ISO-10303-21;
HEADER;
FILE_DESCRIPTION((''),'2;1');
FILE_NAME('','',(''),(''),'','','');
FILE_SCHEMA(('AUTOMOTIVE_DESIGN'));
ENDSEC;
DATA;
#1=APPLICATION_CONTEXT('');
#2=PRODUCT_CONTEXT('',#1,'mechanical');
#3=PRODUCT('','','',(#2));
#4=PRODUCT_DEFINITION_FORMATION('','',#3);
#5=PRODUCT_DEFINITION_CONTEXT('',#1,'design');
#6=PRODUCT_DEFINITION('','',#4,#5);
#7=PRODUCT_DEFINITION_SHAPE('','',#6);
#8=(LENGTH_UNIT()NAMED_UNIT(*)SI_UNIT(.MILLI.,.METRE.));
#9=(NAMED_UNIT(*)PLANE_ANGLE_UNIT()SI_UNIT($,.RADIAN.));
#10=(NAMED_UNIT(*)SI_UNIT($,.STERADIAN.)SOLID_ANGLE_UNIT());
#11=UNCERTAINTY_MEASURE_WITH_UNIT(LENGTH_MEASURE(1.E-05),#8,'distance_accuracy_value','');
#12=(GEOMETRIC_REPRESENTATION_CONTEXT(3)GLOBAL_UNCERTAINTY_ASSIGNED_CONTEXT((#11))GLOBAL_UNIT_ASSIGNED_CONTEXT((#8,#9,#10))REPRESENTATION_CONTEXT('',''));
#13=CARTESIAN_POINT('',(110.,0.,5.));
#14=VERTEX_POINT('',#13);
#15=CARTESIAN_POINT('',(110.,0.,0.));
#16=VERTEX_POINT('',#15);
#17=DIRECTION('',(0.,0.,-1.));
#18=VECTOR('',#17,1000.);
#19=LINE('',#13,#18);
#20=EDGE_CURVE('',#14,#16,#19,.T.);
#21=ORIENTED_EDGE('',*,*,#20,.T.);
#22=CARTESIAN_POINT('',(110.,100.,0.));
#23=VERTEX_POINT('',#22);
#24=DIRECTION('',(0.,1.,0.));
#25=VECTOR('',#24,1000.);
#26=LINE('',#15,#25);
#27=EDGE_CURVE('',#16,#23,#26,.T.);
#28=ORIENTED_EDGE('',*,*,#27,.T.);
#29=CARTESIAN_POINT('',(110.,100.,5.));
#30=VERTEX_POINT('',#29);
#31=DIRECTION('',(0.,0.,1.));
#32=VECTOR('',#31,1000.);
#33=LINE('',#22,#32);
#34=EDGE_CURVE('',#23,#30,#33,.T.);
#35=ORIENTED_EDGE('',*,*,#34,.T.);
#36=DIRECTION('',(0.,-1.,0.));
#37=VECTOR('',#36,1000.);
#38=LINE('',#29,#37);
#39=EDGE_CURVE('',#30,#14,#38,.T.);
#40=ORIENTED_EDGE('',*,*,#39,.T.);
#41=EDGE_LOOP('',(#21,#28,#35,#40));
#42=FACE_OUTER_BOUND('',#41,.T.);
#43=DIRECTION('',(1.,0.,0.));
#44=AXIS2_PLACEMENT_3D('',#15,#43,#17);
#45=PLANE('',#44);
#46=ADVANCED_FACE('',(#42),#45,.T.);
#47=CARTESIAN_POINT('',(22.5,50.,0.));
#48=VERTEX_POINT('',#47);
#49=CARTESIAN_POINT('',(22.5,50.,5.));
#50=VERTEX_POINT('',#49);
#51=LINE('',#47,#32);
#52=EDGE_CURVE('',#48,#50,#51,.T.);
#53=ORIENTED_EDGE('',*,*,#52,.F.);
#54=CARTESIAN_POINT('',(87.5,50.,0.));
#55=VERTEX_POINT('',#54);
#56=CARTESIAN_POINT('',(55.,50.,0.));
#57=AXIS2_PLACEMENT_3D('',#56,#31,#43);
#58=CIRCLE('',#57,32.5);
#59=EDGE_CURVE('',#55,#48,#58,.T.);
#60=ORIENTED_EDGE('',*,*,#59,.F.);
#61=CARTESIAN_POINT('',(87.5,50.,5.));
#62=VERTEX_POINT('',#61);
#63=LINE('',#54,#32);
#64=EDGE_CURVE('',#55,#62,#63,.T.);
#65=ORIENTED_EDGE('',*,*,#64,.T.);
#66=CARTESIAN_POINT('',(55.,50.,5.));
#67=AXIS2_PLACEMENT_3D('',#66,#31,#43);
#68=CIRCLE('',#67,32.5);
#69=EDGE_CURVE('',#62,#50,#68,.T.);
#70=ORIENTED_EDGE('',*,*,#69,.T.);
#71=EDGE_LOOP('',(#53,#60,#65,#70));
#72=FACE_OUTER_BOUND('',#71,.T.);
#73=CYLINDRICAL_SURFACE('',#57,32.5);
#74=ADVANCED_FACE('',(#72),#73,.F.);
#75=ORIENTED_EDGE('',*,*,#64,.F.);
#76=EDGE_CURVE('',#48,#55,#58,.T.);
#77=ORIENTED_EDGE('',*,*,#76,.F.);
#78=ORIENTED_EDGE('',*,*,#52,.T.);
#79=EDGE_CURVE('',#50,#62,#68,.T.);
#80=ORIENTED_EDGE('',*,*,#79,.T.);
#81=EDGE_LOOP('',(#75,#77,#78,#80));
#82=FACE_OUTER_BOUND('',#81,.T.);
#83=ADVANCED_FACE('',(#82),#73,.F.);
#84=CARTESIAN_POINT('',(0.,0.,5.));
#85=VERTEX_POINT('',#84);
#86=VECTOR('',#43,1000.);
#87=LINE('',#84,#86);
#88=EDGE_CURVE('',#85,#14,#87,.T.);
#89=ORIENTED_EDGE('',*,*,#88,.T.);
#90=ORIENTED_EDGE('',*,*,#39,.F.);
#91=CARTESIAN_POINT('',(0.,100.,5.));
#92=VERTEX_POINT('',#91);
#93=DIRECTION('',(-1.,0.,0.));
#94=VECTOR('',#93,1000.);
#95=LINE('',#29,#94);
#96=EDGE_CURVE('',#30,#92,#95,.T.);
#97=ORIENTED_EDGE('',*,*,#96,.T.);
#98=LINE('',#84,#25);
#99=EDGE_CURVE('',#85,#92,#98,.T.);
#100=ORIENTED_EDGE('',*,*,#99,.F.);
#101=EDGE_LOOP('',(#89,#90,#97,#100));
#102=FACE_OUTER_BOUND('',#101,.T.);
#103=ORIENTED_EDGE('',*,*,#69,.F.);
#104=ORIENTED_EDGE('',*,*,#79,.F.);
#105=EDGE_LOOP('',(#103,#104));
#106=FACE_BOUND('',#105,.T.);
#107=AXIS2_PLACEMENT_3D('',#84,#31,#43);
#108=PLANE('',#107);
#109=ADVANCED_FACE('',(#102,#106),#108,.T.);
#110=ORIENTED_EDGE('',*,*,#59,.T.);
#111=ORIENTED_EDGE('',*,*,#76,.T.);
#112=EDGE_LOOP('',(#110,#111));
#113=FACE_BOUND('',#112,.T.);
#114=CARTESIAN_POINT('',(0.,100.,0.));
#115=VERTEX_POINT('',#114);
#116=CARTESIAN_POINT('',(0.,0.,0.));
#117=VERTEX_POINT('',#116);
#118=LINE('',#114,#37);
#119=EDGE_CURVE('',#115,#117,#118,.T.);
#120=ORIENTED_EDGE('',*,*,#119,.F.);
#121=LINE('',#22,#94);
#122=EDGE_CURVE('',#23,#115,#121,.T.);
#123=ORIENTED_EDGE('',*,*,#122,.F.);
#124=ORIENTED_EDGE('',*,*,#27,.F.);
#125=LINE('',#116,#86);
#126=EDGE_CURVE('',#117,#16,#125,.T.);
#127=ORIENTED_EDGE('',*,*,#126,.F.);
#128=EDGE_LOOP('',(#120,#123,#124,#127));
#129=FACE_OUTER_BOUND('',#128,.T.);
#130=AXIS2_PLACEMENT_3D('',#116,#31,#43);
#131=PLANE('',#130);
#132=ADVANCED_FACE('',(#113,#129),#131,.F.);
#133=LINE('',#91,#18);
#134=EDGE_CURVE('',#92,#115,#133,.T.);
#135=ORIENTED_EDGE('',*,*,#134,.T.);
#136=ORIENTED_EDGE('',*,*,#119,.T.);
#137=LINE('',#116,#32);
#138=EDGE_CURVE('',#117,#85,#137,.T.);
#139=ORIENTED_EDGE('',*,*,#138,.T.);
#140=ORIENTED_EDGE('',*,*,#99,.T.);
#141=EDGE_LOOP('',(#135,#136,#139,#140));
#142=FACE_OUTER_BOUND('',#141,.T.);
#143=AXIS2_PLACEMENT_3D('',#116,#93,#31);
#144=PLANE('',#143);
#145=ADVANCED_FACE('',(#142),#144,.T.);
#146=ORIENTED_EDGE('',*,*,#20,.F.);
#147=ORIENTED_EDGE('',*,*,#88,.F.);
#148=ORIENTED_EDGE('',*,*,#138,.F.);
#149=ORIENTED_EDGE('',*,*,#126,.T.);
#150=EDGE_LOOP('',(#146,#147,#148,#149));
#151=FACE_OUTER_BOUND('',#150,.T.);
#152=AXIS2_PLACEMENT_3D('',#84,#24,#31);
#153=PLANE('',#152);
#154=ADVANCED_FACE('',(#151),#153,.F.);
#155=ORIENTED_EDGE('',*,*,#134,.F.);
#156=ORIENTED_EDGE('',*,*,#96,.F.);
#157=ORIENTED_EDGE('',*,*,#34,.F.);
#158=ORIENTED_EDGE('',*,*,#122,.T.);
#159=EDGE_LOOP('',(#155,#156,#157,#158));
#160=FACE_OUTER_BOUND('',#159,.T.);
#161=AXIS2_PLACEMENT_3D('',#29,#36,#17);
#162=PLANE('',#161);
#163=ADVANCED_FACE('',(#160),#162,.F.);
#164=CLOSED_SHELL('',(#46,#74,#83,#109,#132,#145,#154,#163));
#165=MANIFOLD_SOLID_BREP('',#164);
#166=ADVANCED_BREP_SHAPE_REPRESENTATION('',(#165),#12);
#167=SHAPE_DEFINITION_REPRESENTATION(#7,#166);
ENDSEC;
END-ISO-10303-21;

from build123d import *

# Parameters (mm, degrees)
SKETCH_1_W          = 110
SKETCH_1_H          = 100
EXTRUDE_1_DEPTH     = 5
CUT_EXTRUDE_1_DEPTH = 5
SKETCH_3_W          = 5
SKETCH_3_H          = 100
EXTRUDE_2_DEPTH     = 50
SKETCH_4_W          = 5
SKETCH_4_H          = 100
EXTRUDE_3_DEPTH     = 50
SKETCH_5_W          = 5
SKETCH_5_H          = 100
CUT_EXTRUDE_2_DEPTH = 50
SKETCH_7_W          = 5
SKETCH_7_H          = 100
CUT_EXTRUDE_3_DEPTH = 50


with BuildPart() as part:
    # 草图1 → 凸台-拉伸1 (new body)
    with BuildSketch(Plane.XY):
        with Locations((55, 50)):
            Rectangle(SKETCH_1_W, SKETCH_1_H)
    extrude(amount=EXTRUDE_1_DEPTH)

    # 草图2 → 切除-拉伸1 (cut)
    with BuildSketch(Plane.XY.offset(5)):
        with BuildLine():
            Line((55, 50), (79.048052385, 71.861865805))
            ThreePointArc((79.048052385, 71.861865805), (68.147991507, 79.72171461), (55, 82.5))
            Line((55, 82.5), (55, 50))
        make_face()
        with BuildLine():
            Line((30.951947615, 28.138134195), (55, 50))
            Line((55, 50), (55, 82.5))
            ThreePointArc((55, 82.5), (25.27828539, 63.147991507), (30.951947615, 28.138134195))
        make_face()
        with BuildLine():
            ThreePointArc((87.5, 50), (85.313459903, 61.719391995), (79.048052385, 71.861865805))
            Line((79.048052385, 71.861865805), (55, 50))
            Line((55, 50), (30.951947615, 28.138134195))
            ThreePointArc((30.951947615, 28.138134195), (66.719391995, 19.686540097), (87.5, 50))
        make_face()
    extrude(amount=-CUT_EXTRUDE_1_DEPTH, mode=Mode.SUBTRACT)

    # 草图3 → 凸台-拉伸2 (add)
    with BuildSketch(Plane(origin=(110, 0, 0), x_dir=(0, 0, -1), z_dir=(1, 0, 0))):
        with Locations((-2.5, 50)):
            Rectangle(SKETCH_3_W, SKETCH_3_H)
    extrude(amount=EXTRUDE_2_DEPTH)

    # 草图4 → 凸台-拉伸3 (add)
    with BuildSketch(Plane.ZY):
        with Locations((2.5, 50)):
            Rectangle(SKETCH_4_W, SKETCH_4_H)
    extrude(amount=EXTRUDE_3_DEPTH)

    # 草图5 → 切除-拉伸2 (cut)
    with BuildSketch(Plane(origin=(160, 0, 0), x_dir=(0, 0, -1), z_dir=(1, 0, 0))):
        with Locations((-2.5, 50)):
            Rectangle(SKETCH_5_W, SKETCH_5_H)
    extrude(amount=-CUT_EXTRUDE_2_DEPTH, mode=Mode.SUBTRACT)

    # 草图7 → 切除-拉伸3 (cut)
    with BuildSketch(Plane.ZY.offset(50)):
        with Locations((2.5, 50)):
            Rectangle(SKETCH_7_W, SKETCH_7_H)
    extrude(amount=-CUT_EXTRUDE_3_DEPTH, mode=Mode.SUBTRACT)


solid = part.part
